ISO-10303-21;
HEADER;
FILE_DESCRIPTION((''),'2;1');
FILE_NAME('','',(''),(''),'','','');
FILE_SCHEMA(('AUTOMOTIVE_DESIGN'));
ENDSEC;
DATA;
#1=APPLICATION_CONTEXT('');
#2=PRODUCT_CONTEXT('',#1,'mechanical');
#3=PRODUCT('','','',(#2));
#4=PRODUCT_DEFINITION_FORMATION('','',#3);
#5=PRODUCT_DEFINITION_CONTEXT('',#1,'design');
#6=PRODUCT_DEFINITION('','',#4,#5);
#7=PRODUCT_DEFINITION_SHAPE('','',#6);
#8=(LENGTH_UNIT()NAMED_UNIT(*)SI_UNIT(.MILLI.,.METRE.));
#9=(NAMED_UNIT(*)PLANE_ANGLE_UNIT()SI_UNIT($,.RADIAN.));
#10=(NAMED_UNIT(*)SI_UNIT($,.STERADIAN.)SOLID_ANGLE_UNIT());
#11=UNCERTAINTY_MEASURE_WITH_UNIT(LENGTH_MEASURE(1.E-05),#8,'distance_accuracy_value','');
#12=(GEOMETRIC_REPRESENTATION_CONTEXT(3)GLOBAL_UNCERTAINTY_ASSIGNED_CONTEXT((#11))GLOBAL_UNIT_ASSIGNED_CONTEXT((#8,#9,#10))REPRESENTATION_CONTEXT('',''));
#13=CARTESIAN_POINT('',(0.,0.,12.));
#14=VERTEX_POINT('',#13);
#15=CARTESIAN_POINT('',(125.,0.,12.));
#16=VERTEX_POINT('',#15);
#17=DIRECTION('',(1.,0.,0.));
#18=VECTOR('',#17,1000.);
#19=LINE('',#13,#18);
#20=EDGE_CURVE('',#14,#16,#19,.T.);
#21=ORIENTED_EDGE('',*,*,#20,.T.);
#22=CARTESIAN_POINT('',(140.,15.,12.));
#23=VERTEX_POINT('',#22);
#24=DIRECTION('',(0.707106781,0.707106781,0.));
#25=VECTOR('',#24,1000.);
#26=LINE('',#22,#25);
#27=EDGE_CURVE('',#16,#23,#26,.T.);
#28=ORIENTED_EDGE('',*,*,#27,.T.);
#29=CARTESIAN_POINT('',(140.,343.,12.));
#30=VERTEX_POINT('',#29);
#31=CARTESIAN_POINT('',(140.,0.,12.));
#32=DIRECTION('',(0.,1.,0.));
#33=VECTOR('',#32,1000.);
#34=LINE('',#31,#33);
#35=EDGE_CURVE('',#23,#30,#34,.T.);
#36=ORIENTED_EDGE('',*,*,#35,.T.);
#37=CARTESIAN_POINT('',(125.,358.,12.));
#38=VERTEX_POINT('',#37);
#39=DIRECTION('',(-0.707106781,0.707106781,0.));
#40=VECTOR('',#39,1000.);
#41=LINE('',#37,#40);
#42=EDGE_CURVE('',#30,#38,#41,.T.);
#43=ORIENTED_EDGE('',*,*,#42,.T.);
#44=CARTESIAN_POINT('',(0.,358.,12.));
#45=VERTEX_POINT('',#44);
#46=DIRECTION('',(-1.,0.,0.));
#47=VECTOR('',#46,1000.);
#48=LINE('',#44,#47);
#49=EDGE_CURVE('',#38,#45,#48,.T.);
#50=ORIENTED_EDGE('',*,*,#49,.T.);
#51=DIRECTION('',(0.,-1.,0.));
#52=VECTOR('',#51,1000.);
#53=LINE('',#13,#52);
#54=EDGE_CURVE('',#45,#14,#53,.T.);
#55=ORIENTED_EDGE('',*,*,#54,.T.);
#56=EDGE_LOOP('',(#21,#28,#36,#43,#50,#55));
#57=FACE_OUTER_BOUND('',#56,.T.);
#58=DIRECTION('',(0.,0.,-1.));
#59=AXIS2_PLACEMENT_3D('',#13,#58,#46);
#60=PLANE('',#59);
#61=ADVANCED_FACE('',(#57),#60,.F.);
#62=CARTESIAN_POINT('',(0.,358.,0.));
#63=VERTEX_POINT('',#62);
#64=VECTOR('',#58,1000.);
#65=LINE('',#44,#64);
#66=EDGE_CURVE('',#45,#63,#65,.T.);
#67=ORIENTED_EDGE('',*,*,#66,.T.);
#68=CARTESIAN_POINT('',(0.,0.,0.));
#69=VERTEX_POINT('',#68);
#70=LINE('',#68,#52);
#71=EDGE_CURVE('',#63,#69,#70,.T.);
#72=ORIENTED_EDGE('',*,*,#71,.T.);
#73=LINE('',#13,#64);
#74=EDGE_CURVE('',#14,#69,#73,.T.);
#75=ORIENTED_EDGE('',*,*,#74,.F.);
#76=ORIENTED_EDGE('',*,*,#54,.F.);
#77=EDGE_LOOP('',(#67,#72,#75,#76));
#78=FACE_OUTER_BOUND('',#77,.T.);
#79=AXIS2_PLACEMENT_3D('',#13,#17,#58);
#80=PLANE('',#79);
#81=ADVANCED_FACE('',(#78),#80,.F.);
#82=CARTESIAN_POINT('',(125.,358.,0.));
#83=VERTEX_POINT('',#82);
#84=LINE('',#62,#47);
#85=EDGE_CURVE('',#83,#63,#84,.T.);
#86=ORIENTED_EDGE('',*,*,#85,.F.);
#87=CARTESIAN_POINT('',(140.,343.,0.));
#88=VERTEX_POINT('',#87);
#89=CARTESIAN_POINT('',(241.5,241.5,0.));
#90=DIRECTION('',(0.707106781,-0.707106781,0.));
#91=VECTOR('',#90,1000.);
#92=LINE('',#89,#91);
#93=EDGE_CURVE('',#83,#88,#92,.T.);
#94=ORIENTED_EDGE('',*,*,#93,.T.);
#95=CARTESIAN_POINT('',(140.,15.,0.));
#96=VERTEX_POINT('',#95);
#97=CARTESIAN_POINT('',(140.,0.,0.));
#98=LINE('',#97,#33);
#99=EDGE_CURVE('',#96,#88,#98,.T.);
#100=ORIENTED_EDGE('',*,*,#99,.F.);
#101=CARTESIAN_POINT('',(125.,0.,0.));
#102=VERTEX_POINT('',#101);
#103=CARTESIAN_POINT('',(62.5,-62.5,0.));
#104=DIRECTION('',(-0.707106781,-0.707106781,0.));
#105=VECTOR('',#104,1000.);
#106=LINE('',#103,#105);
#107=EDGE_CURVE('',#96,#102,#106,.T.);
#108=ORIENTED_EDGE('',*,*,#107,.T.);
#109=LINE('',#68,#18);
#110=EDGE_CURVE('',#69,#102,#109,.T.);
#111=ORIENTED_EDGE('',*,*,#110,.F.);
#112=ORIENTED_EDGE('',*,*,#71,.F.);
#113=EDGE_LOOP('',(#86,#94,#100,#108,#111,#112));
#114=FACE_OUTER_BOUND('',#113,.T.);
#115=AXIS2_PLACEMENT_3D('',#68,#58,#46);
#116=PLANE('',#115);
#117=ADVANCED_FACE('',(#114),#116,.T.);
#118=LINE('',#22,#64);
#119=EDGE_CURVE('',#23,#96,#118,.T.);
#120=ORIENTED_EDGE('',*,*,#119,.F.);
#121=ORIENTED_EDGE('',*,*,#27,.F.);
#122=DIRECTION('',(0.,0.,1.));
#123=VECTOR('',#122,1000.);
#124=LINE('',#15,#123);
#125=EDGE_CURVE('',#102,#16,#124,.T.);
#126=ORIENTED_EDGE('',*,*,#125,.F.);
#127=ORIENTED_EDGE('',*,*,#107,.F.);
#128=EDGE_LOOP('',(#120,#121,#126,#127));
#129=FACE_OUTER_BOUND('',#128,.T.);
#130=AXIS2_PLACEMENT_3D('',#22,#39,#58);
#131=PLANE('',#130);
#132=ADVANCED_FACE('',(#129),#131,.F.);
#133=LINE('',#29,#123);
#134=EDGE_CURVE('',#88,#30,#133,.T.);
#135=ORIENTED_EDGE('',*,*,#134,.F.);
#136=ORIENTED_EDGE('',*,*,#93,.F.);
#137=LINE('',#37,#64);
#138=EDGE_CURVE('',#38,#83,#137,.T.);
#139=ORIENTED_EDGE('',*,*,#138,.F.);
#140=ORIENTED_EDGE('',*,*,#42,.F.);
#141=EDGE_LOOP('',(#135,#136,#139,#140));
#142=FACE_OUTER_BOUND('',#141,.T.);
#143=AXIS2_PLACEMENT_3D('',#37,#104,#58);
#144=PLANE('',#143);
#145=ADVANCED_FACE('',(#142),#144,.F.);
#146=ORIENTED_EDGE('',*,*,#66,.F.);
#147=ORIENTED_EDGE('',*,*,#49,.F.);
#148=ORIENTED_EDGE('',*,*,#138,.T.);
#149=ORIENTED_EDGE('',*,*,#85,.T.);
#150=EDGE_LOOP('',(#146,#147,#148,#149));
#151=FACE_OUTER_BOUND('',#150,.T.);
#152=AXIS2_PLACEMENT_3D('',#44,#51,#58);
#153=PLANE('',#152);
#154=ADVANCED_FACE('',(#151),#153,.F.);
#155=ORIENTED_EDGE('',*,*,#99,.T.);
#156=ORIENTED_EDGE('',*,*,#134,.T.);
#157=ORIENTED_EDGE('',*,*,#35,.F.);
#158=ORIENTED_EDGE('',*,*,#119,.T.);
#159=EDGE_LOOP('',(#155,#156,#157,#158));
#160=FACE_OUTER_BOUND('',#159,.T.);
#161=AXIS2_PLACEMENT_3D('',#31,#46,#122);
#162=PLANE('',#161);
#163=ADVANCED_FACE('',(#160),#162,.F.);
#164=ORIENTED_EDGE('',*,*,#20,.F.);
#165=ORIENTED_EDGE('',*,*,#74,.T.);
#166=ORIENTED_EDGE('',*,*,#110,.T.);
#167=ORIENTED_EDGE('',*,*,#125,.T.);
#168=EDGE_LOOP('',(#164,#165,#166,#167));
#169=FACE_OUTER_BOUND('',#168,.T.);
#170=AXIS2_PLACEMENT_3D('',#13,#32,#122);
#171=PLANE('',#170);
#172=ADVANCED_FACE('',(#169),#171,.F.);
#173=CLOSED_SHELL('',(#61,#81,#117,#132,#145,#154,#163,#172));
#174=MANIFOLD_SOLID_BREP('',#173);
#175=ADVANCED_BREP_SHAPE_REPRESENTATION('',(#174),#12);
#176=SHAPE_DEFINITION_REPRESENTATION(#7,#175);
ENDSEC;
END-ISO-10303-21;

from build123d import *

# Parameters (mm, degrees)
SKETCH1_W           = 140
SKETCH1_H           = 358
BOSS_EXTRUDE1_DEPTH = 12
CHAMFER2_SIZE       = 15


with BuildPart() as part:
    # Sketch1 → Boss-Extrude1 (new body)
    with BuildSketch(Plane.XY):
        with Locations((70, 179)):
            Rectangle(SKETCH1_W, SKETCH1_H)
    extrude(amount=BOSS_EXTRUDE1_DEPTH)

    # Chamfer2
    chamfer2_edges = [part.edges().sort_by_distance(p)[0] for p in [
        (140, 358, 6),
        (140, 0, 6),
    ]]
    chamfer(chamfer2_edges, length=CHAMFER2_SIZE)


solid = part.part
